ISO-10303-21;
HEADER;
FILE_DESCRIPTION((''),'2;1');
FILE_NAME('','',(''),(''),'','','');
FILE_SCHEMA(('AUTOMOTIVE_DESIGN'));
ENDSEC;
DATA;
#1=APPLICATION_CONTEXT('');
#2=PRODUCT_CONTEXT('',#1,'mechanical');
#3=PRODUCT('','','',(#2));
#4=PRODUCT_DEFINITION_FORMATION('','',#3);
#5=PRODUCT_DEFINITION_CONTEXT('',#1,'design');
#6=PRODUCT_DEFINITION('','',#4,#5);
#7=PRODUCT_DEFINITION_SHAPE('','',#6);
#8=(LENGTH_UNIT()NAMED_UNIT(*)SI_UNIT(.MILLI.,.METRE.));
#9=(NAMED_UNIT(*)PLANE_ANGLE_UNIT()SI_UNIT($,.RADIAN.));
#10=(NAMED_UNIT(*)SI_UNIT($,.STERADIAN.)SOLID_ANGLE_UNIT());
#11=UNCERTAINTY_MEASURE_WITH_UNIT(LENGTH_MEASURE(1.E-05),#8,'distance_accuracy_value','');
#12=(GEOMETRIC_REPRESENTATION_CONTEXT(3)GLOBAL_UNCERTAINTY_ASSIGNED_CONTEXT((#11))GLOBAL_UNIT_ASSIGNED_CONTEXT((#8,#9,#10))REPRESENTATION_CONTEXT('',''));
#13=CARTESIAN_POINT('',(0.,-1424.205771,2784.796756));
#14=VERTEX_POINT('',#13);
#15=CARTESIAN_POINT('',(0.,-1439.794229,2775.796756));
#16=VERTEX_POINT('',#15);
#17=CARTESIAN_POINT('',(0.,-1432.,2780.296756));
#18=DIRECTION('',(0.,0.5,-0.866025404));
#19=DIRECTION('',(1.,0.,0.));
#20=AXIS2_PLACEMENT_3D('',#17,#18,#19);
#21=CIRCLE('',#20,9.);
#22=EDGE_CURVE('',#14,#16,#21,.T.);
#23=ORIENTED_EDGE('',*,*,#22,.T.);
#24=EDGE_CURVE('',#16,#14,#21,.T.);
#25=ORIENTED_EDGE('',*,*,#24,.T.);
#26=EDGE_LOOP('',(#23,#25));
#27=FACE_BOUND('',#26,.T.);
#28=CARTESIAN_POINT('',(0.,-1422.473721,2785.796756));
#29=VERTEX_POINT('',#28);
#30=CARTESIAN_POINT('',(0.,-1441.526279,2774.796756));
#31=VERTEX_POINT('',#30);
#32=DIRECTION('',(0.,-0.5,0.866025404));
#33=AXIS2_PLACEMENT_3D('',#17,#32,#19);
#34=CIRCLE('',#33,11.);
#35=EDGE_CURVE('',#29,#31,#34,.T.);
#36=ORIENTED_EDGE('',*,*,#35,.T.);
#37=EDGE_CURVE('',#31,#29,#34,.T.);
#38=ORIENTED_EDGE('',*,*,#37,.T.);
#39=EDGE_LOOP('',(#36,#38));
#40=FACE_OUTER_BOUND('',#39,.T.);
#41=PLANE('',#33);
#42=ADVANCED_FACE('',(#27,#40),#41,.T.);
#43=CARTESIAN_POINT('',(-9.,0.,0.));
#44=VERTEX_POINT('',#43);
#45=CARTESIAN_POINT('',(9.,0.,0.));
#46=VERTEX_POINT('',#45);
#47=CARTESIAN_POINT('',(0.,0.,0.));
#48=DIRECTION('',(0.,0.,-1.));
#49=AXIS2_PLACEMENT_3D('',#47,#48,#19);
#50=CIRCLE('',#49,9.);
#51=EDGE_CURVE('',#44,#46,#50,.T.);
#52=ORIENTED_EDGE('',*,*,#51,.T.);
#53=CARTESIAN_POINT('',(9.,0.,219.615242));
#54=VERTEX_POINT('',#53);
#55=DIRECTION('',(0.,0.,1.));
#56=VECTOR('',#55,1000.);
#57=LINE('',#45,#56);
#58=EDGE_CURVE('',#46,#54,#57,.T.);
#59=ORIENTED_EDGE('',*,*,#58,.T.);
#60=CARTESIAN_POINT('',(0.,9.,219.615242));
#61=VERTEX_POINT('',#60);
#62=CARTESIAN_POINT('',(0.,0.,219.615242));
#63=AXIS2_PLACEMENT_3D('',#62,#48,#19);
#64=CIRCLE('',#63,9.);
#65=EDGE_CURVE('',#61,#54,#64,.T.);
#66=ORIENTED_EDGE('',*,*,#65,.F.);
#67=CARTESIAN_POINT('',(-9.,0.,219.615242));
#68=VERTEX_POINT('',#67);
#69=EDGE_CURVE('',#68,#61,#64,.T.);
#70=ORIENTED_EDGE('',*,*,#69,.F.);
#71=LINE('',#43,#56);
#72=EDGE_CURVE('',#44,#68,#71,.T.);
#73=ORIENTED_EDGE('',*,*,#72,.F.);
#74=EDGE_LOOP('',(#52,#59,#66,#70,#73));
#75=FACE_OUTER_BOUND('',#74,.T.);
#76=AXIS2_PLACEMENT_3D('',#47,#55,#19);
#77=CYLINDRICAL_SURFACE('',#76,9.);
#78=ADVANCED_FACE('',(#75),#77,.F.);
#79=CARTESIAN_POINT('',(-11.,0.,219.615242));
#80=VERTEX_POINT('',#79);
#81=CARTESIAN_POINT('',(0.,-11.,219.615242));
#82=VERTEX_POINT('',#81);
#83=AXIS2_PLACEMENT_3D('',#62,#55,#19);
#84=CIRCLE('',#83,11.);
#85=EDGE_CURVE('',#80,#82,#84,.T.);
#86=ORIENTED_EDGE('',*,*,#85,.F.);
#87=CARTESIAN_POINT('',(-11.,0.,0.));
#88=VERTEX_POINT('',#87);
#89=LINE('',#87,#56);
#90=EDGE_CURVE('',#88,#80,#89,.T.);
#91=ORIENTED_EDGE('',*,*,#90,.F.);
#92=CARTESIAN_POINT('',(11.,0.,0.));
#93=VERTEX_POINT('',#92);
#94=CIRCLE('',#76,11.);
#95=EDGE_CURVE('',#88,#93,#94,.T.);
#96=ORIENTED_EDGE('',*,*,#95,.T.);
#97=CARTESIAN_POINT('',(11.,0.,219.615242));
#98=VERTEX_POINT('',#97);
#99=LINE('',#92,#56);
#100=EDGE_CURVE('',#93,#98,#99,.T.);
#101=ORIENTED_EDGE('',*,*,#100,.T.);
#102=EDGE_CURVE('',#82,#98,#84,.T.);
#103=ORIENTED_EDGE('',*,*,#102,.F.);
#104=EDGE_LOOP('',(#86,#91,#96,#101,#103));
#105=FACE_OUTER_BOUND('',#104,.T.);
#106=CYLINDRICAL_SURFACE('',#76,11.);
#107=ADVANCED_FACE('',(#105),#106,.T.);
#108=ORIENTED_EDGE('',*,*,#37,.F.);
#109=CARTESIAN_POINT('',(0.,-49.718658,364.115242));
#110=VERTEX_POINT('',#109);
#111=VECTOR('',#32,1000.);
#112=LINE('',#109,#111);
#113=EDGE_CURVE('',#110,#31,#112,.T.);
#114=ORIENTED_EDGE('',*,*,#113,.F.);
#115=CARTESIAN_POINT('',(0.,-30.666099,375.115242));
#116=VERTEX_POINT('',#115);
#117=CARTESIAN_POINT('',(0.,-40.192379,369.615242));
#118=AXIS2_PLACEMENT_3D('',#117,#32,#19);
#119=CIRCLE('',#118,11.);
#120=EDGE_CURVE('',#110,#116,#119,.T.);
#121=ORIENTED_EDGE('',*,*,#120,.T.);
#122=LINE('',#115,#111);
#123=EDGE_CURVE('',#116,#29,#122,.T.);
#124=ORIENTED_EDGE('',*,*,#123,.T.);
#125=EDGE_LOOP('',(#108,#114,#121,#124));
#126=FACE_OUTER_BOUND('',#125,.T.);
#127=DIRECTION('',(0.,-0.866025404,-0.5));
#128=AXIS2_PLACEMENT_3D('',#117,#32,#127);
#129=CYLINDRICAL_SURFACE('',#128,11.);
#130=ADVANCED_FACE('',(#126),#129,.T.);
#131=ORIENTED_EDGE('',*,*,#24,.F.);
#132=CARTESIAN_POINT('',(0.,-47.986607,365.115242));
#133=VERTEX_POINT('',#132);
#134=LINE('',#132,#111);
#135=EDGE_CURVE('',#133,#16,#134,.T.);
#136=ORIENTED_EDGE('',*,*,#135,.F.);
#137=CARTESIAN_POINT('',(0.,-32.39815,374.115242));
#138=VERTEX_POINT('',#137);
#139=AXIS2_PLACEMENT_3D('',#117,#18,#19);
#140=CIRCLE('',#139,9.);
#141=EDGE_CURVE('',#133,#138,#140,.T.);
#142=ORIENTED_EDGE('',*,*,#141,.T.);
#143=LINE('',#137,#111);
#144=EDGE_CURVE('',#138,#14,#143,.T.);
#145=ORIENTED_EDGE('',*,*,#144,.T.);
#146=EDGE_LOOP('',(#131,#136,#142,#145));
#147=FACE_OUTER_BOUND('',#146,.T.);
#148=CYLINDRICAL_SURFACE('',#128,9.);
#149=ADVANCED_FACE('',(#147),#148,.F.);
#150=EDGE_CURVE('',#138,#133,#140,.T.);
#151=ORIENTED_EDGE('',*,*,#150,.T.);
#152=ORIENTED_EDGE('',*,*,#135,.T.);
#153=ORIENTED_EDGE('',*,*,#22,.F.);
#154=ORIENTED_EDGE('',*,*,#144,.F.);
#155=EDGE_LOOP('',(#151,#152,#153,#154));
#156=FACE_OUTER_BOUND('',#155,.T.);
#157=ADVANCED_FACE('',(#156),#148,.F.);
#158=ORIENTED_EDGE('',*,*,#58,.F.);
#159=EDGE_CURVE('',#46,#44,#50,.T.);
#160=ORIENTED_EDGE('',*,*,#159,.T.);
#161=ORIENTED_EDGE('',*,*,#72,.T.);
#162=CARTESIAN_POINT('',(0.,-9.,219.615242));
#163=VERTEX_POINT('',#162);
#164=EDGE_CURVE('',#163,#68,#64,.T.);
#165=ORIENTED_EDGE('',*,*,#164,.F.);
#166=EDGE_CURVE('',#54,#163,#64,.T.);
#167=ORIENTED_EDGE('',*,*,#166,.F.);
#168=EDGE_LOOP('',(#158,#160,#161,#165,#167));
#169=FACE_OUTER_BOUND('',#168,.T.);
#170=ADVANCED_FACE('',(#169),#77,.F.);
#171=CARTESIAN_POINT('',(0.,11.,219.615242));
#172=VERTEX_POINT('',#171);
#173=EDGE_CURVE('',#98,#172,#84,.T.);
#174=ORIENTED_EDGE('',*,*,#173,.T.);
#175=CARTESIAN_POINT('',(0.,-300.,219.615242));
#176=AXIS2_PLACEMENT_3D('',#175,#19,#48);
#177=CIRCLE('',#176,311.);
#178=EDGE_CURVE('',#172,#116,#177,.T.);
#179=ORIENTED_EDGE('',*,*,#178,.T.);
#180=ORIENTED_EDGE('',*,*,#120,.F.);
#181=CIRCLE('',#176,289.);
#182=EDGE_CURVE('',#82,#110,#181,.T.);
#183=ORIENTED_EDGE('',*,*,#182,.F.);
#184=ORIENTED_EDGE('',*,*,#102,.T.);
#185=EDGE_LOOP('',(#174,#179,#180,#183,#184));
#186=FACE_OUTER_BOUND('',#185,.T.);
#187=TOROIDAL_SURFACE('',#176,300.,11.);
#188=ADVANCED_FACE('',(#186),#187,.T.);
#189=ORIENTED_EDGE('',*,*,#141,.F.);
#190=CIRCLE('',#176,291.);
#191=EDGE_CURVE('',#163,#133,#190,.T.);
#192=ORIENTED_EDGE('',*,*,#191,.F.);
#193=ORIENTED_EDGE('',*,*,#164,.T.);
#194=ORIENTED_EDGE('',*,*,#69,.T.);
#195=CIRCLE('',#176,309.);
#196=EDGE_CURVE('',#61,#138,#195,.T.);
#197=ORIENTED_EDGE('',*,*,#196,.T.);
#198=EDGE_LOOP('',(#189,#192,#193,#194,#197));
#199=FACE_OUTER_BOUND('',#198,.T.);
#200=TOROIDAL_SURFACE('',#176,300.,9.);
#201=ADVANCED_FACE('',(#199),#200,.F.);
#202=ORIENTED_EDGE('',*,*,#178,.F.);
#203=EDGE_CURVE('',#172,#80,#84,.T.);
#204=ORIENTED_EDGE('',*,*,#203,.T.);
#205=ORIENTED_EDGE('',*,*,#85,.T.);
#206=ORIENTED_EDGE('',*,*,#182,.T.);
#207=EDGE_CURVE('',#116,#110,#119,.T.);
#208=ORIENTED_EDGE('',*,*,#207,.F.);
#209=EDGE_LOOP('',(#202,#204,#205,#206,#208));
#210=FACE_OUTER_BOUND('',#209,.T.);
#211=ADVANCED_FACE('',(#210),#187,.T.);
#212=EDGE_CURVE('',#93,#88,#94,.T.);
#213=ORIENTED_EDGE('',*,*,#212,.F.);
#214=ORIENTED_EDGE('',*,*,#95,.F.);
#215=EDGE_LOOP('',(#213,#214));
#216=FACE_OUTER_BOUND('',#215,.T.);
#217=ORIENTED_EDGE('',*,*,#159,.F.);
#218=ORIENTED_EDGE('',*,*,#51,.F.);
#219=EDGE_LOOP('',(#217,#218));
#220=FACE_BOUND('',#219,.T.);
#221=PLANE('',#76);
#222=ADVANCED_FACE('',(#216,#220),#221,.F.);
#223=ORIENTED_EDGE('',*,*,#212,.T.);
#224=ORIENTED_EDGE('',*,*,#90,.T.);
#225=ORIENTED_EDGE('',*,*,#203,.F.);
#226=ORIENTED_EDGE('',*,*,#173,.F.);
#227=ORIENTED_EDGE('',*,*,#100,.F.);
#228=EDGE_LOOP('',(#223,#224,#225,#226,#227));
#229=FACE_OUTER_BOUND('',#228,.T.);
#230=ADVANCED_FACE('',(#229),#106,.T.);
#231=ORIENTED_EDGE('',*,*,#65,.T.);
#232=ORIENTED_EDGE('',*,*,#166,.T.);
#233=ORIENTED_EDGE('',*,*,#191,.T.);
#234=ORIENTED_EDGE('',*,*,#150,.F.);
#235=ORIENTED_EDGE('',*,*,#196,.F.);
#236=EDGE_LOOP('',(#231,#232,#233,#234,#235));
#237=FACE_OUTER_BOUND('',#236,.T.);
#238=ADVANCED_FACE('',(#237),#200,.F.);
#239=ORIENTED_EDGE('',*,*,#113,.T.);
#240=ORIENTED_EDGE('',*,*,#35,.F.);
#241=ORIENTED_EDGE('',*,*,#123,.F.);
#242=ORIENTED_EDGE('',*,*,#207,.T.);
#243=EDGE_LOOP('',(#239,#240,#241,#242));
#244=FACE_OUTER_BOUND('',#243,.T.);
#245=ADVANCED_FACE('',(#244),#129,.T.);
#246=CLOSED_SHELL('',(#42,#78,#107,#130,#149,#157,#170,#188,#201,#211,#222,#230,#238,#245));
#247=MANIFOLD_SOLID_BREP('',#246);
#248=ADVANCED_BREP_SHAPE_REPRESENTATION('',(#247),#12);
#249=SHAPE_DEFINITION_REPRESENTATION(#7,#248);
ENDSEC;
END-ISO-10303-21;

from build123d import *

# Parameters (mm, degrees)
SKETCH1_R   = 11
SKETCH1_R_2 = 9


with BuildPart() as part:
    # Sweep1: sweep along a path in Sketch2
    with BuildLine(Plane(origin=(0, 0, 0), x_dir=(0, 0, -1), z_dir=(1, 0, 0))) as sweep1_path:
        Line((0, 0), (-219.615242271, 0))
        ThreePointArc((-219.615242271, 0), (-297.260955801, -10.222252113), (-369.615242271, -40.192378865))
        Line((-369.615242271, -40.192378865), (-2780.296756439, -1432))
    # Sketch1 → Sweep1 (sweep)
    with BuildSketch(Plane.XY):
        Circle(SKETCH1_R)
        Circle(SKETCH1_R_2, mode=Mode.SUBTRACT)
    sweep(path=sweep1_path.line)


solid = part.part
